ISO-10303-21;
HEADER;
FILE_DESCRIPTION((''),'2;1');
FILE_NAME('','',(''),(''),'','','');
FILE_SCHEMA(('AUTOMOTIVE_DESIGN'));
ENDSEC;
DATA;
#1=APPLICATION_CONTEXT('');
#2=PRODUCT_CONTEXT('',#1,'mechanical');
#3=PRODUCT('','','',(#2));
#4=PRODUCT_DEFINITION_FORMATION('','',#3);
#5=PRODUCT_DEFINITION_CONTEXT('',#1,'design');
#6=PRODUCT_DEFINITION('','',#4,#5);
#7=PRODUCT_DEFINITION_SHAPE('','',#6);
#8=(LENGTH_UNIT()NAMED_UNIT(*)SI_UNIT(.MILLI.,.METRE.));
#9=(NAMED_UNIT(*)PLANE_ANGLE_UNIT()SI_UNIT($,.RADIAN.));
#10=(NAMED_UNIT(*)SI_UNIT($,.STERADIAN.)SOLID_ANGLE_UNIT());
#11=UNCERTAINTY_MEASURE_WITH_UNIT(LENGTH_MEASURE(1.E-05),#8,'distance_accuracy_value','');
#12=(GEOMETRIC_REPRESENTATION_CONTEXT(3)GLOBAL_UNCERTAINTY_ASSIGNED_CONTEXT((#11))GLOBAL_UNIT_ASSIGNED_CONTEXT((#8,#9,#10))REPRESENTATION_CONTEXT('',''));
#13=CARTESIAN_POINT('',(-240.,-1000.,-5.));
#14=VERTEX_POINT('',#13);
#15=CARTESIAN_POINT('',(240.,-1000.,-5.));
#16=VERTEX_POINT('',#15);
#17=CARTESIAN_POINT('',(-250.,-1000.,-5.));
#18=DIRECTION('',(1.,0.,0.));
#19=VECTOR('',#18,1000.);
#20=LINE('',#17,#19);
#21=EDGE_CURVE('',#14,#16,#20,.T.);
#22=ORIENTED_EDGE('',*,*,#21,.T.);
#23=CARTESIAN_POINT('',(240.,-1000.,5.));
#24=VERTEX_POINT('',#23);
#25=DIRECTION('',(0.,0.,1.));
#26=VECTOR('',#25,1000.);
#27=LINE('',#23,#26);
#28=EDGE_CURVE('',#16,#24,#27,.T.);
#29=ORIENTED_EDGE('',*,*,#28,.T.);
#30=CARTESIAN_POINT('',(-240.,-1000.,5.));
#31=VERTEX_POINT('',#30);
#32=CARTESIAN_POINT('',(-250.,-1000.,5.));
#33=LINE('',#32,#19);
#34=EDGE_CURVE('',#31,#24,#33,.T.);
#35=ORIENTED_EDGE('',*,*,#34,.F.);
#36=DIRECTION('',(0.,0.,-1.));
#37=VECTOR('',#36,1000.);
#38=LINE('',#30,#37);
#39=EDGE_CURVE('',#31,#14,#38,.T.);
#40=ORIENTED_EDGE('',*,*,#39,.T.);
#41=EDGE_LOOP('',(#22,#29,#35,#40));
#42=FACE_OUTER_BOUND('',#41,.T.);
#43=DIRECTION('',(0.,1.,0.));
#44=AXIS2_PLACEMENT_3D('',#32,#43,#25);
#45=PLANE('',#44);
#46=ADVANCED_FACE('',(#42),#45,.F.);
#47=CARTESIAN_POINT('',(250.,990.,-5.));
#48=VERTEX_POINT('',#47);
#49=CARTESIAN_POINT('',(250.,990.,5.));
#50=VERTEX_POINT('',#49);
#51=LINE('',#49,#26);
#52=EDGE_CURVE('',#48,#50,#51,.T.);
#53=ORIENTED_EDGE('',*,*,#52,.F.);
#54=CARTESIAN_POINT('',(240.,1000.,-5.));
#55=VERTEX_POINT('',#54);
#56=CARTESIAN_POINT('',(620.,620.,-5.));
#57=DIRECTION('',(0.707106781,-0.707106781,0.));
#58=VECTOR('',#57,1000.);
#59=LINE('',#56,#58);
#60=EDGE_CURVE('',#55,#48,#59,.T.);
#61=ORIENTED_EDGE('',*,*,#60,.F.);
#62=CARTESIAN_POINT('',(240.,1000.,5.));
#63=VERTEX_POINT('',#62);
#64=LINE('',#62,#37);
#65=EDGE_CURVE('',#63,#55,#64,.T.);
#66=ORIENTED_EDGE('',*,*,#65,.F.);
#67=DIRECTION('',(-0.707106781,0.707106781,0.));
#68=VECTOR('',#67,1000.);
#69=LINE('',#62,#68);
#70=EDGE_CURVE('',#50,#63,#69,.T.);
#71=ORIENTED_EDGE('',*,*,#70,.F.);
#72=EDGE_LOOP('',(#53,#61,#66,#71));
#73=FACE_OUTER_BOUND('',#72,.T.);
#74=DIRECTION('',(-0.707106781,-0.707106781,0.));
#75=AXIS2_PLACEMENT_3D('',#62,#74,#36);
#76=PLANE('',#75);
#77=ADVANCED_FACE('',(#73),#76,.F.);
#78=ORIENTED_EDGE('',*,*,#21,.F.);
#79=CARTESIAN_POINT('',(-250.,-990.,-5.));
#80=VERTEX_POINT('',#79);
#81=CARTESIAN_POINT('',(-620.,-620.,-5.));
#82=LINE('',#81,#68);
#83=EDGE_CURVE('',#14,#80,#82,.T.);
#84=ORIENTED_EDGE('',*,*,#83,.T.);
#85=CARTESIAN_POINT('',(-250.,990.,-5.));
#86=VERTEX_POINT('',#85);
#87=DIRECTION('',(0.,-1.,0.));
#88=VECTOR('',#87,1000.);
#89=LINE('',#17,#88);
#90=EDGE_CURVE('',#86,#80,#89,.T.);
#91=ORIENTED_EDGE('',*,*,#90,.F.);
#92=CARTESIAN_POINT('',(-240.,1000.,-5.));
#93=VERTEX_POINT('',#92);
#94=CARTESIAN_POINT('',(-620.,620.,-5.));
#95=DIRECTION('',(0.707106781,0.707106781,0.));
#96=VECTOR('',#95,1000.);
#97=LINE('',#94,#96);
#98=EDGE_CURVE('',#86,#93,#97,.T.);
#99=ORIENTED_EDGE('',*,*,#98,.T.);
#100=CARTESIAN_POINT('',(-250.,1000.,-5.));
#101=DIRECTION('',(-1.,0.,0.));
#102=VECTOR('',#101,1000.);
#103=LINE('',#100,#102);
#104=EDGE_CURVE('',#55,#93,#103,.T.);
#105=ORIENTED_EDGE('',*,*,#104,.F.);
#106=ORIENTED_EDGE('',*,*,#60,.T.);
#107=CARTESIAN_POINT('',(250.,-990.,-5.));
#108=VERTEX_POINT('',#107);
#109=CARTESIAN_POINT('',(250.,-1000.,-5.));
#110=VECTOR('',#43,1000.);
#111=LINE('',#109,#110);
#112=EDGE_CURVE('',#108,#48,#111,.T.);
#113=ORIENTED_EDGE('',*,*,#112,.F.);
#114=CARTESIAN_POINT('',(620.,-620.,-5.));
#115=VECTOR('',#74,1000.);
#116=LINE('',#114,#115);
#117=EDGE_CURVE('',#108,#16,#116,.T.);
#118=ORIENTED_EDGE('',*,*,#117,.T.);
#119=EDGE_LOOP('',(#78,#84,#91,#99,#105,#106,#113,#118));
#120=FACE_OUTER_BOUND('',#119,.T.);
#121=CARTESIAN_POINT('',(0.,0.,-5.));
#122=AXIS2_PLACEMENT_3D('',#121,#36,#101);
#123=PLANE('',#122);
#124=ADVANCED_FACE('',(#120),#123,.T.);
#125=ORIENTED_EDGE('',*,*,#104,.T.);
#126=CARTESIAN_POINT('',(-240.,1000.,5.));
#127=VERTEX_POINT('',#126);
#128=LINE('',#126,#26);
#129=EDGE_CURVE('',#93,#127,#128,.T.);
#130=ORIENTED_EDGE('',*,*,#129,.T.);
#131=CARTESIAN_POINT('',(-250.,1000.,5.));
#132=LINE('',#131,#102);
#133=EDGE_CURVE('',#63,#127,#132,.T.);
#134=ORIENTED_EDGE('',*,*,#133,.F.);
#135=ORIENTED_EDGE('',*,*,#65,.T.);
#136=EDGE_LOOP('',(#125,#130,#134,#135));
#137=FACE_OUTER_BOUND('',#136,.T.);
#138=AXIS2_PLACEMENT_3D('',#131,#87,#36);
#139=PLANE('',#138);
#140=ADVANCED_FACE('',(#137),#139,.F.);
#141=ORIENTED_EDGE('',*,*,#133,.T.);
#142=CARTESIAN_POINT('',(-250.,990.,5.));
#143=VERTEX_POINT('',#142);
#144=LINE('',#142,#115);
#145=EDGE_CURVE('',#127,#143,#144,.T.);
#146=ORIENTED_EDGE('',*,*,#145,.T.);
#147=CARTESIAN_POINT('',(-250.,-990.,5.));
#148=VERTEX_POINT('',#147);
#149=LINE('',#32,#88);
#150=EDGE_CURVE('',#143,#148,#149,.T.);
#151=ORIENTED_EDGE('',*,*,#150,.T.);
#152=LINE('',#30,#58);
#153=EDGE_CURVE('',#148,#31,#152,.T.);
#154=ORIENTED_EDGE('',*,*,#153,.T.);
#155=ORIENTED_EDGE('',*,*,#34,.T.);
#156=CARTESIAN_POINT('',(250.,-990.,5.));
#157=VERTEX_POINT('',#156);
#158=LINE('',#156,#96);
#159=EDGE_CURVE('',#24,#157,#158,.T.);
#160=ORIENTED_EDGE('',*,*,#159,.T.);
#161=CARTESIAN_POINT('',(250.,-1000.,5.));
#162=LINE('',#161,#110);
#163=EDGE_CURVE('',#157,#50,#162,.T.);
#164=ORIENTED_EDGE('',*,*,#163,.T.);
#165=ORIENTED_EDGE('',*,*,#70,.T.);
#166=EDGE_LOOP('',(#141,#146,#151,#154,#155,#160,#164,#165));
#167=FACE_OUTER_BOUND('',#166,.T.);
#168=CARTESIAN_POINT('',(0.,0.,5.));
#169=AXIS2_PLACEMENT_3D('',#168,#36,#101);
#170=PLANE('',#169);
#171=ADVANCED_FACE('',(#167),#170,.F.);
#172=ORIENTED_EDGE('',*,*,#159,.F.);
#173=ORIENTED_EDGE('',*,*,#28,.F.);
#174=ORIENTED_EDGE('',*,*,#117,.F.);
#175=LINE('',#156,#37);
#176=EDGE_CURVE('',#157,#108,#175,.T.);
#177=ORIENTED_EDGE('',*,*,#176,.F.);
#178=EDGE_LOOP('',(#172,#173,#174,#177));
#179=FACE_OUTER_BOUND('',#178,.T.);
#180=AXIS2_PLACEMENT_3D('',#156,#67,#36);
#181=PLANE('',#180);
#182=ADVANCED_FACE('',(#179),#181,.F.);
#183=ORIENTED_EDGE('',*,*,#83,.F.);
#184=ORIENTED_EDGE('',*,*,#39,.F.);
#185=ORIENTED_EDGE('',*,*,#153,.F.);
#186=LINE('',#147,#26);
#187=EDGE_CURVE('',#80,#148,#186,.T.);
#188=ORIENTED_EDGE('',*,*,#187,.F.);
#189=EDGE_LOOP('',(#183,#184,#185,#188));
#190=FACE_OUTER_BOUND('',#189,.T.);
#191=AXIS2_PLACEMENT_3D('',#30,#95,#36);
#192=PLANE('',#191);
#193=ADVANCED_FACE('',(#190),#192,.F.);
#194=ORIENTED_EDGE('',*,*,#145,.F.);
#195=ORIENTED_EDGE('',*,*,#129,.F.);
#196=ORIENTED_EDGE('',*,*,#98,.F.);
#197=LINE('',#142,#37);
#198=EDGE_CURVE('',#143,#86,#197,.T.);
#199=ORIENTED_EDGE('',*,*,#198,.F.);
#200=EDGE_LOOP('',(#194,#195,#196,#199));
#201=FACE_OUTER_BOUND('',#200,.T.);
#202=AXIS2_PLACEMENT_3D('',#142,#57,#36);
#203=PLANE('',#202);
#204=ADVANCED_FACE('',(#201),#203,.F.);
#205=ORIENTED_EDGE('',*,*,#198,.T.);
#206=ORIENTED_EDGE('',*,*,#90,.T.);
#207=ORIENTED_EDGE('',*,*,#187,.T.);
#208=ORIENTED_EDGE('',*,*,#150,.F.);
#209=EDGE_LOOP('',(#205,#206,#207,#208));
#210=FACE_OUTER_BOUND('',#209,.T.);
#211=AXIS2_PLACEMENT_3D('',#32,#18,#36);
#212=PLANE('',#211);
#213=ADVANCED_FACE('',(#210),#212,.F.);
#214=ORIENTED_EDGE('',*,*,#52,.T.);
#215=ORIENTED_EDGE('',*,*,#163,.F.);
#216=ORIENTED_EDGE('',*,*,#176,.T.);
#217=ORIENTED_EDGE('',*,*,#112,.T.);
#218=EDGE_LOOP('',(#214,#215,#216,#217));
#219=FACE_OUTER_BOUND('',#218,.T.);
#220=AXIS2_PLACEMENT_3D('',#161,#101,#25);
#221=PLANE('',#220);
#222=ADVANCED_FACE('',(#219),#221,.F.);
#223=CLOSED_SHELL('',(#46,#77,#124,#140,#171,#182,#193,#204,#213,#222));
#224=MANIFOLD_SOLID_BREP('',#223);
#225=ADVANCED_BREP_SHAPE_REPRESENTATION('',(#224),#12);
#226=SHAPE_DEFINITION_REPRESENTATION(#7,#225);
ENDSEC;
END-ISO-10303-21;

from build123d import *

# Parameters (mm, degrees)
SKETCH_1_W      = 500
SKETCH_1_H      = 2000
EXTRUDE_1_DEPTH = 5
CHAMFER_1_SIZE  = 10


with BuildPart() as part:
    # 草图1 → 凸台-拉伸1 (new, symmetric)
    with BuildSketch(Plane.XY):
        Rectangle(SKETCH_1_W, SKETCH_1_H)
    extrude(amount=EXTRUDE_1_DEPTH, both=True)

    # 倒角1
    chamfer_1_edges = [part.edges().sort_by_distance(p)[0] for p in [
        (250, -1000, 0),
        (-250, -1000, 0),
        (-250, 1000, 0),
        (250, 1000, 0),
    ]]
    chamfer(chamfer_1_edges, length=CHAMFER_1_SIZE)


solid = part.part
